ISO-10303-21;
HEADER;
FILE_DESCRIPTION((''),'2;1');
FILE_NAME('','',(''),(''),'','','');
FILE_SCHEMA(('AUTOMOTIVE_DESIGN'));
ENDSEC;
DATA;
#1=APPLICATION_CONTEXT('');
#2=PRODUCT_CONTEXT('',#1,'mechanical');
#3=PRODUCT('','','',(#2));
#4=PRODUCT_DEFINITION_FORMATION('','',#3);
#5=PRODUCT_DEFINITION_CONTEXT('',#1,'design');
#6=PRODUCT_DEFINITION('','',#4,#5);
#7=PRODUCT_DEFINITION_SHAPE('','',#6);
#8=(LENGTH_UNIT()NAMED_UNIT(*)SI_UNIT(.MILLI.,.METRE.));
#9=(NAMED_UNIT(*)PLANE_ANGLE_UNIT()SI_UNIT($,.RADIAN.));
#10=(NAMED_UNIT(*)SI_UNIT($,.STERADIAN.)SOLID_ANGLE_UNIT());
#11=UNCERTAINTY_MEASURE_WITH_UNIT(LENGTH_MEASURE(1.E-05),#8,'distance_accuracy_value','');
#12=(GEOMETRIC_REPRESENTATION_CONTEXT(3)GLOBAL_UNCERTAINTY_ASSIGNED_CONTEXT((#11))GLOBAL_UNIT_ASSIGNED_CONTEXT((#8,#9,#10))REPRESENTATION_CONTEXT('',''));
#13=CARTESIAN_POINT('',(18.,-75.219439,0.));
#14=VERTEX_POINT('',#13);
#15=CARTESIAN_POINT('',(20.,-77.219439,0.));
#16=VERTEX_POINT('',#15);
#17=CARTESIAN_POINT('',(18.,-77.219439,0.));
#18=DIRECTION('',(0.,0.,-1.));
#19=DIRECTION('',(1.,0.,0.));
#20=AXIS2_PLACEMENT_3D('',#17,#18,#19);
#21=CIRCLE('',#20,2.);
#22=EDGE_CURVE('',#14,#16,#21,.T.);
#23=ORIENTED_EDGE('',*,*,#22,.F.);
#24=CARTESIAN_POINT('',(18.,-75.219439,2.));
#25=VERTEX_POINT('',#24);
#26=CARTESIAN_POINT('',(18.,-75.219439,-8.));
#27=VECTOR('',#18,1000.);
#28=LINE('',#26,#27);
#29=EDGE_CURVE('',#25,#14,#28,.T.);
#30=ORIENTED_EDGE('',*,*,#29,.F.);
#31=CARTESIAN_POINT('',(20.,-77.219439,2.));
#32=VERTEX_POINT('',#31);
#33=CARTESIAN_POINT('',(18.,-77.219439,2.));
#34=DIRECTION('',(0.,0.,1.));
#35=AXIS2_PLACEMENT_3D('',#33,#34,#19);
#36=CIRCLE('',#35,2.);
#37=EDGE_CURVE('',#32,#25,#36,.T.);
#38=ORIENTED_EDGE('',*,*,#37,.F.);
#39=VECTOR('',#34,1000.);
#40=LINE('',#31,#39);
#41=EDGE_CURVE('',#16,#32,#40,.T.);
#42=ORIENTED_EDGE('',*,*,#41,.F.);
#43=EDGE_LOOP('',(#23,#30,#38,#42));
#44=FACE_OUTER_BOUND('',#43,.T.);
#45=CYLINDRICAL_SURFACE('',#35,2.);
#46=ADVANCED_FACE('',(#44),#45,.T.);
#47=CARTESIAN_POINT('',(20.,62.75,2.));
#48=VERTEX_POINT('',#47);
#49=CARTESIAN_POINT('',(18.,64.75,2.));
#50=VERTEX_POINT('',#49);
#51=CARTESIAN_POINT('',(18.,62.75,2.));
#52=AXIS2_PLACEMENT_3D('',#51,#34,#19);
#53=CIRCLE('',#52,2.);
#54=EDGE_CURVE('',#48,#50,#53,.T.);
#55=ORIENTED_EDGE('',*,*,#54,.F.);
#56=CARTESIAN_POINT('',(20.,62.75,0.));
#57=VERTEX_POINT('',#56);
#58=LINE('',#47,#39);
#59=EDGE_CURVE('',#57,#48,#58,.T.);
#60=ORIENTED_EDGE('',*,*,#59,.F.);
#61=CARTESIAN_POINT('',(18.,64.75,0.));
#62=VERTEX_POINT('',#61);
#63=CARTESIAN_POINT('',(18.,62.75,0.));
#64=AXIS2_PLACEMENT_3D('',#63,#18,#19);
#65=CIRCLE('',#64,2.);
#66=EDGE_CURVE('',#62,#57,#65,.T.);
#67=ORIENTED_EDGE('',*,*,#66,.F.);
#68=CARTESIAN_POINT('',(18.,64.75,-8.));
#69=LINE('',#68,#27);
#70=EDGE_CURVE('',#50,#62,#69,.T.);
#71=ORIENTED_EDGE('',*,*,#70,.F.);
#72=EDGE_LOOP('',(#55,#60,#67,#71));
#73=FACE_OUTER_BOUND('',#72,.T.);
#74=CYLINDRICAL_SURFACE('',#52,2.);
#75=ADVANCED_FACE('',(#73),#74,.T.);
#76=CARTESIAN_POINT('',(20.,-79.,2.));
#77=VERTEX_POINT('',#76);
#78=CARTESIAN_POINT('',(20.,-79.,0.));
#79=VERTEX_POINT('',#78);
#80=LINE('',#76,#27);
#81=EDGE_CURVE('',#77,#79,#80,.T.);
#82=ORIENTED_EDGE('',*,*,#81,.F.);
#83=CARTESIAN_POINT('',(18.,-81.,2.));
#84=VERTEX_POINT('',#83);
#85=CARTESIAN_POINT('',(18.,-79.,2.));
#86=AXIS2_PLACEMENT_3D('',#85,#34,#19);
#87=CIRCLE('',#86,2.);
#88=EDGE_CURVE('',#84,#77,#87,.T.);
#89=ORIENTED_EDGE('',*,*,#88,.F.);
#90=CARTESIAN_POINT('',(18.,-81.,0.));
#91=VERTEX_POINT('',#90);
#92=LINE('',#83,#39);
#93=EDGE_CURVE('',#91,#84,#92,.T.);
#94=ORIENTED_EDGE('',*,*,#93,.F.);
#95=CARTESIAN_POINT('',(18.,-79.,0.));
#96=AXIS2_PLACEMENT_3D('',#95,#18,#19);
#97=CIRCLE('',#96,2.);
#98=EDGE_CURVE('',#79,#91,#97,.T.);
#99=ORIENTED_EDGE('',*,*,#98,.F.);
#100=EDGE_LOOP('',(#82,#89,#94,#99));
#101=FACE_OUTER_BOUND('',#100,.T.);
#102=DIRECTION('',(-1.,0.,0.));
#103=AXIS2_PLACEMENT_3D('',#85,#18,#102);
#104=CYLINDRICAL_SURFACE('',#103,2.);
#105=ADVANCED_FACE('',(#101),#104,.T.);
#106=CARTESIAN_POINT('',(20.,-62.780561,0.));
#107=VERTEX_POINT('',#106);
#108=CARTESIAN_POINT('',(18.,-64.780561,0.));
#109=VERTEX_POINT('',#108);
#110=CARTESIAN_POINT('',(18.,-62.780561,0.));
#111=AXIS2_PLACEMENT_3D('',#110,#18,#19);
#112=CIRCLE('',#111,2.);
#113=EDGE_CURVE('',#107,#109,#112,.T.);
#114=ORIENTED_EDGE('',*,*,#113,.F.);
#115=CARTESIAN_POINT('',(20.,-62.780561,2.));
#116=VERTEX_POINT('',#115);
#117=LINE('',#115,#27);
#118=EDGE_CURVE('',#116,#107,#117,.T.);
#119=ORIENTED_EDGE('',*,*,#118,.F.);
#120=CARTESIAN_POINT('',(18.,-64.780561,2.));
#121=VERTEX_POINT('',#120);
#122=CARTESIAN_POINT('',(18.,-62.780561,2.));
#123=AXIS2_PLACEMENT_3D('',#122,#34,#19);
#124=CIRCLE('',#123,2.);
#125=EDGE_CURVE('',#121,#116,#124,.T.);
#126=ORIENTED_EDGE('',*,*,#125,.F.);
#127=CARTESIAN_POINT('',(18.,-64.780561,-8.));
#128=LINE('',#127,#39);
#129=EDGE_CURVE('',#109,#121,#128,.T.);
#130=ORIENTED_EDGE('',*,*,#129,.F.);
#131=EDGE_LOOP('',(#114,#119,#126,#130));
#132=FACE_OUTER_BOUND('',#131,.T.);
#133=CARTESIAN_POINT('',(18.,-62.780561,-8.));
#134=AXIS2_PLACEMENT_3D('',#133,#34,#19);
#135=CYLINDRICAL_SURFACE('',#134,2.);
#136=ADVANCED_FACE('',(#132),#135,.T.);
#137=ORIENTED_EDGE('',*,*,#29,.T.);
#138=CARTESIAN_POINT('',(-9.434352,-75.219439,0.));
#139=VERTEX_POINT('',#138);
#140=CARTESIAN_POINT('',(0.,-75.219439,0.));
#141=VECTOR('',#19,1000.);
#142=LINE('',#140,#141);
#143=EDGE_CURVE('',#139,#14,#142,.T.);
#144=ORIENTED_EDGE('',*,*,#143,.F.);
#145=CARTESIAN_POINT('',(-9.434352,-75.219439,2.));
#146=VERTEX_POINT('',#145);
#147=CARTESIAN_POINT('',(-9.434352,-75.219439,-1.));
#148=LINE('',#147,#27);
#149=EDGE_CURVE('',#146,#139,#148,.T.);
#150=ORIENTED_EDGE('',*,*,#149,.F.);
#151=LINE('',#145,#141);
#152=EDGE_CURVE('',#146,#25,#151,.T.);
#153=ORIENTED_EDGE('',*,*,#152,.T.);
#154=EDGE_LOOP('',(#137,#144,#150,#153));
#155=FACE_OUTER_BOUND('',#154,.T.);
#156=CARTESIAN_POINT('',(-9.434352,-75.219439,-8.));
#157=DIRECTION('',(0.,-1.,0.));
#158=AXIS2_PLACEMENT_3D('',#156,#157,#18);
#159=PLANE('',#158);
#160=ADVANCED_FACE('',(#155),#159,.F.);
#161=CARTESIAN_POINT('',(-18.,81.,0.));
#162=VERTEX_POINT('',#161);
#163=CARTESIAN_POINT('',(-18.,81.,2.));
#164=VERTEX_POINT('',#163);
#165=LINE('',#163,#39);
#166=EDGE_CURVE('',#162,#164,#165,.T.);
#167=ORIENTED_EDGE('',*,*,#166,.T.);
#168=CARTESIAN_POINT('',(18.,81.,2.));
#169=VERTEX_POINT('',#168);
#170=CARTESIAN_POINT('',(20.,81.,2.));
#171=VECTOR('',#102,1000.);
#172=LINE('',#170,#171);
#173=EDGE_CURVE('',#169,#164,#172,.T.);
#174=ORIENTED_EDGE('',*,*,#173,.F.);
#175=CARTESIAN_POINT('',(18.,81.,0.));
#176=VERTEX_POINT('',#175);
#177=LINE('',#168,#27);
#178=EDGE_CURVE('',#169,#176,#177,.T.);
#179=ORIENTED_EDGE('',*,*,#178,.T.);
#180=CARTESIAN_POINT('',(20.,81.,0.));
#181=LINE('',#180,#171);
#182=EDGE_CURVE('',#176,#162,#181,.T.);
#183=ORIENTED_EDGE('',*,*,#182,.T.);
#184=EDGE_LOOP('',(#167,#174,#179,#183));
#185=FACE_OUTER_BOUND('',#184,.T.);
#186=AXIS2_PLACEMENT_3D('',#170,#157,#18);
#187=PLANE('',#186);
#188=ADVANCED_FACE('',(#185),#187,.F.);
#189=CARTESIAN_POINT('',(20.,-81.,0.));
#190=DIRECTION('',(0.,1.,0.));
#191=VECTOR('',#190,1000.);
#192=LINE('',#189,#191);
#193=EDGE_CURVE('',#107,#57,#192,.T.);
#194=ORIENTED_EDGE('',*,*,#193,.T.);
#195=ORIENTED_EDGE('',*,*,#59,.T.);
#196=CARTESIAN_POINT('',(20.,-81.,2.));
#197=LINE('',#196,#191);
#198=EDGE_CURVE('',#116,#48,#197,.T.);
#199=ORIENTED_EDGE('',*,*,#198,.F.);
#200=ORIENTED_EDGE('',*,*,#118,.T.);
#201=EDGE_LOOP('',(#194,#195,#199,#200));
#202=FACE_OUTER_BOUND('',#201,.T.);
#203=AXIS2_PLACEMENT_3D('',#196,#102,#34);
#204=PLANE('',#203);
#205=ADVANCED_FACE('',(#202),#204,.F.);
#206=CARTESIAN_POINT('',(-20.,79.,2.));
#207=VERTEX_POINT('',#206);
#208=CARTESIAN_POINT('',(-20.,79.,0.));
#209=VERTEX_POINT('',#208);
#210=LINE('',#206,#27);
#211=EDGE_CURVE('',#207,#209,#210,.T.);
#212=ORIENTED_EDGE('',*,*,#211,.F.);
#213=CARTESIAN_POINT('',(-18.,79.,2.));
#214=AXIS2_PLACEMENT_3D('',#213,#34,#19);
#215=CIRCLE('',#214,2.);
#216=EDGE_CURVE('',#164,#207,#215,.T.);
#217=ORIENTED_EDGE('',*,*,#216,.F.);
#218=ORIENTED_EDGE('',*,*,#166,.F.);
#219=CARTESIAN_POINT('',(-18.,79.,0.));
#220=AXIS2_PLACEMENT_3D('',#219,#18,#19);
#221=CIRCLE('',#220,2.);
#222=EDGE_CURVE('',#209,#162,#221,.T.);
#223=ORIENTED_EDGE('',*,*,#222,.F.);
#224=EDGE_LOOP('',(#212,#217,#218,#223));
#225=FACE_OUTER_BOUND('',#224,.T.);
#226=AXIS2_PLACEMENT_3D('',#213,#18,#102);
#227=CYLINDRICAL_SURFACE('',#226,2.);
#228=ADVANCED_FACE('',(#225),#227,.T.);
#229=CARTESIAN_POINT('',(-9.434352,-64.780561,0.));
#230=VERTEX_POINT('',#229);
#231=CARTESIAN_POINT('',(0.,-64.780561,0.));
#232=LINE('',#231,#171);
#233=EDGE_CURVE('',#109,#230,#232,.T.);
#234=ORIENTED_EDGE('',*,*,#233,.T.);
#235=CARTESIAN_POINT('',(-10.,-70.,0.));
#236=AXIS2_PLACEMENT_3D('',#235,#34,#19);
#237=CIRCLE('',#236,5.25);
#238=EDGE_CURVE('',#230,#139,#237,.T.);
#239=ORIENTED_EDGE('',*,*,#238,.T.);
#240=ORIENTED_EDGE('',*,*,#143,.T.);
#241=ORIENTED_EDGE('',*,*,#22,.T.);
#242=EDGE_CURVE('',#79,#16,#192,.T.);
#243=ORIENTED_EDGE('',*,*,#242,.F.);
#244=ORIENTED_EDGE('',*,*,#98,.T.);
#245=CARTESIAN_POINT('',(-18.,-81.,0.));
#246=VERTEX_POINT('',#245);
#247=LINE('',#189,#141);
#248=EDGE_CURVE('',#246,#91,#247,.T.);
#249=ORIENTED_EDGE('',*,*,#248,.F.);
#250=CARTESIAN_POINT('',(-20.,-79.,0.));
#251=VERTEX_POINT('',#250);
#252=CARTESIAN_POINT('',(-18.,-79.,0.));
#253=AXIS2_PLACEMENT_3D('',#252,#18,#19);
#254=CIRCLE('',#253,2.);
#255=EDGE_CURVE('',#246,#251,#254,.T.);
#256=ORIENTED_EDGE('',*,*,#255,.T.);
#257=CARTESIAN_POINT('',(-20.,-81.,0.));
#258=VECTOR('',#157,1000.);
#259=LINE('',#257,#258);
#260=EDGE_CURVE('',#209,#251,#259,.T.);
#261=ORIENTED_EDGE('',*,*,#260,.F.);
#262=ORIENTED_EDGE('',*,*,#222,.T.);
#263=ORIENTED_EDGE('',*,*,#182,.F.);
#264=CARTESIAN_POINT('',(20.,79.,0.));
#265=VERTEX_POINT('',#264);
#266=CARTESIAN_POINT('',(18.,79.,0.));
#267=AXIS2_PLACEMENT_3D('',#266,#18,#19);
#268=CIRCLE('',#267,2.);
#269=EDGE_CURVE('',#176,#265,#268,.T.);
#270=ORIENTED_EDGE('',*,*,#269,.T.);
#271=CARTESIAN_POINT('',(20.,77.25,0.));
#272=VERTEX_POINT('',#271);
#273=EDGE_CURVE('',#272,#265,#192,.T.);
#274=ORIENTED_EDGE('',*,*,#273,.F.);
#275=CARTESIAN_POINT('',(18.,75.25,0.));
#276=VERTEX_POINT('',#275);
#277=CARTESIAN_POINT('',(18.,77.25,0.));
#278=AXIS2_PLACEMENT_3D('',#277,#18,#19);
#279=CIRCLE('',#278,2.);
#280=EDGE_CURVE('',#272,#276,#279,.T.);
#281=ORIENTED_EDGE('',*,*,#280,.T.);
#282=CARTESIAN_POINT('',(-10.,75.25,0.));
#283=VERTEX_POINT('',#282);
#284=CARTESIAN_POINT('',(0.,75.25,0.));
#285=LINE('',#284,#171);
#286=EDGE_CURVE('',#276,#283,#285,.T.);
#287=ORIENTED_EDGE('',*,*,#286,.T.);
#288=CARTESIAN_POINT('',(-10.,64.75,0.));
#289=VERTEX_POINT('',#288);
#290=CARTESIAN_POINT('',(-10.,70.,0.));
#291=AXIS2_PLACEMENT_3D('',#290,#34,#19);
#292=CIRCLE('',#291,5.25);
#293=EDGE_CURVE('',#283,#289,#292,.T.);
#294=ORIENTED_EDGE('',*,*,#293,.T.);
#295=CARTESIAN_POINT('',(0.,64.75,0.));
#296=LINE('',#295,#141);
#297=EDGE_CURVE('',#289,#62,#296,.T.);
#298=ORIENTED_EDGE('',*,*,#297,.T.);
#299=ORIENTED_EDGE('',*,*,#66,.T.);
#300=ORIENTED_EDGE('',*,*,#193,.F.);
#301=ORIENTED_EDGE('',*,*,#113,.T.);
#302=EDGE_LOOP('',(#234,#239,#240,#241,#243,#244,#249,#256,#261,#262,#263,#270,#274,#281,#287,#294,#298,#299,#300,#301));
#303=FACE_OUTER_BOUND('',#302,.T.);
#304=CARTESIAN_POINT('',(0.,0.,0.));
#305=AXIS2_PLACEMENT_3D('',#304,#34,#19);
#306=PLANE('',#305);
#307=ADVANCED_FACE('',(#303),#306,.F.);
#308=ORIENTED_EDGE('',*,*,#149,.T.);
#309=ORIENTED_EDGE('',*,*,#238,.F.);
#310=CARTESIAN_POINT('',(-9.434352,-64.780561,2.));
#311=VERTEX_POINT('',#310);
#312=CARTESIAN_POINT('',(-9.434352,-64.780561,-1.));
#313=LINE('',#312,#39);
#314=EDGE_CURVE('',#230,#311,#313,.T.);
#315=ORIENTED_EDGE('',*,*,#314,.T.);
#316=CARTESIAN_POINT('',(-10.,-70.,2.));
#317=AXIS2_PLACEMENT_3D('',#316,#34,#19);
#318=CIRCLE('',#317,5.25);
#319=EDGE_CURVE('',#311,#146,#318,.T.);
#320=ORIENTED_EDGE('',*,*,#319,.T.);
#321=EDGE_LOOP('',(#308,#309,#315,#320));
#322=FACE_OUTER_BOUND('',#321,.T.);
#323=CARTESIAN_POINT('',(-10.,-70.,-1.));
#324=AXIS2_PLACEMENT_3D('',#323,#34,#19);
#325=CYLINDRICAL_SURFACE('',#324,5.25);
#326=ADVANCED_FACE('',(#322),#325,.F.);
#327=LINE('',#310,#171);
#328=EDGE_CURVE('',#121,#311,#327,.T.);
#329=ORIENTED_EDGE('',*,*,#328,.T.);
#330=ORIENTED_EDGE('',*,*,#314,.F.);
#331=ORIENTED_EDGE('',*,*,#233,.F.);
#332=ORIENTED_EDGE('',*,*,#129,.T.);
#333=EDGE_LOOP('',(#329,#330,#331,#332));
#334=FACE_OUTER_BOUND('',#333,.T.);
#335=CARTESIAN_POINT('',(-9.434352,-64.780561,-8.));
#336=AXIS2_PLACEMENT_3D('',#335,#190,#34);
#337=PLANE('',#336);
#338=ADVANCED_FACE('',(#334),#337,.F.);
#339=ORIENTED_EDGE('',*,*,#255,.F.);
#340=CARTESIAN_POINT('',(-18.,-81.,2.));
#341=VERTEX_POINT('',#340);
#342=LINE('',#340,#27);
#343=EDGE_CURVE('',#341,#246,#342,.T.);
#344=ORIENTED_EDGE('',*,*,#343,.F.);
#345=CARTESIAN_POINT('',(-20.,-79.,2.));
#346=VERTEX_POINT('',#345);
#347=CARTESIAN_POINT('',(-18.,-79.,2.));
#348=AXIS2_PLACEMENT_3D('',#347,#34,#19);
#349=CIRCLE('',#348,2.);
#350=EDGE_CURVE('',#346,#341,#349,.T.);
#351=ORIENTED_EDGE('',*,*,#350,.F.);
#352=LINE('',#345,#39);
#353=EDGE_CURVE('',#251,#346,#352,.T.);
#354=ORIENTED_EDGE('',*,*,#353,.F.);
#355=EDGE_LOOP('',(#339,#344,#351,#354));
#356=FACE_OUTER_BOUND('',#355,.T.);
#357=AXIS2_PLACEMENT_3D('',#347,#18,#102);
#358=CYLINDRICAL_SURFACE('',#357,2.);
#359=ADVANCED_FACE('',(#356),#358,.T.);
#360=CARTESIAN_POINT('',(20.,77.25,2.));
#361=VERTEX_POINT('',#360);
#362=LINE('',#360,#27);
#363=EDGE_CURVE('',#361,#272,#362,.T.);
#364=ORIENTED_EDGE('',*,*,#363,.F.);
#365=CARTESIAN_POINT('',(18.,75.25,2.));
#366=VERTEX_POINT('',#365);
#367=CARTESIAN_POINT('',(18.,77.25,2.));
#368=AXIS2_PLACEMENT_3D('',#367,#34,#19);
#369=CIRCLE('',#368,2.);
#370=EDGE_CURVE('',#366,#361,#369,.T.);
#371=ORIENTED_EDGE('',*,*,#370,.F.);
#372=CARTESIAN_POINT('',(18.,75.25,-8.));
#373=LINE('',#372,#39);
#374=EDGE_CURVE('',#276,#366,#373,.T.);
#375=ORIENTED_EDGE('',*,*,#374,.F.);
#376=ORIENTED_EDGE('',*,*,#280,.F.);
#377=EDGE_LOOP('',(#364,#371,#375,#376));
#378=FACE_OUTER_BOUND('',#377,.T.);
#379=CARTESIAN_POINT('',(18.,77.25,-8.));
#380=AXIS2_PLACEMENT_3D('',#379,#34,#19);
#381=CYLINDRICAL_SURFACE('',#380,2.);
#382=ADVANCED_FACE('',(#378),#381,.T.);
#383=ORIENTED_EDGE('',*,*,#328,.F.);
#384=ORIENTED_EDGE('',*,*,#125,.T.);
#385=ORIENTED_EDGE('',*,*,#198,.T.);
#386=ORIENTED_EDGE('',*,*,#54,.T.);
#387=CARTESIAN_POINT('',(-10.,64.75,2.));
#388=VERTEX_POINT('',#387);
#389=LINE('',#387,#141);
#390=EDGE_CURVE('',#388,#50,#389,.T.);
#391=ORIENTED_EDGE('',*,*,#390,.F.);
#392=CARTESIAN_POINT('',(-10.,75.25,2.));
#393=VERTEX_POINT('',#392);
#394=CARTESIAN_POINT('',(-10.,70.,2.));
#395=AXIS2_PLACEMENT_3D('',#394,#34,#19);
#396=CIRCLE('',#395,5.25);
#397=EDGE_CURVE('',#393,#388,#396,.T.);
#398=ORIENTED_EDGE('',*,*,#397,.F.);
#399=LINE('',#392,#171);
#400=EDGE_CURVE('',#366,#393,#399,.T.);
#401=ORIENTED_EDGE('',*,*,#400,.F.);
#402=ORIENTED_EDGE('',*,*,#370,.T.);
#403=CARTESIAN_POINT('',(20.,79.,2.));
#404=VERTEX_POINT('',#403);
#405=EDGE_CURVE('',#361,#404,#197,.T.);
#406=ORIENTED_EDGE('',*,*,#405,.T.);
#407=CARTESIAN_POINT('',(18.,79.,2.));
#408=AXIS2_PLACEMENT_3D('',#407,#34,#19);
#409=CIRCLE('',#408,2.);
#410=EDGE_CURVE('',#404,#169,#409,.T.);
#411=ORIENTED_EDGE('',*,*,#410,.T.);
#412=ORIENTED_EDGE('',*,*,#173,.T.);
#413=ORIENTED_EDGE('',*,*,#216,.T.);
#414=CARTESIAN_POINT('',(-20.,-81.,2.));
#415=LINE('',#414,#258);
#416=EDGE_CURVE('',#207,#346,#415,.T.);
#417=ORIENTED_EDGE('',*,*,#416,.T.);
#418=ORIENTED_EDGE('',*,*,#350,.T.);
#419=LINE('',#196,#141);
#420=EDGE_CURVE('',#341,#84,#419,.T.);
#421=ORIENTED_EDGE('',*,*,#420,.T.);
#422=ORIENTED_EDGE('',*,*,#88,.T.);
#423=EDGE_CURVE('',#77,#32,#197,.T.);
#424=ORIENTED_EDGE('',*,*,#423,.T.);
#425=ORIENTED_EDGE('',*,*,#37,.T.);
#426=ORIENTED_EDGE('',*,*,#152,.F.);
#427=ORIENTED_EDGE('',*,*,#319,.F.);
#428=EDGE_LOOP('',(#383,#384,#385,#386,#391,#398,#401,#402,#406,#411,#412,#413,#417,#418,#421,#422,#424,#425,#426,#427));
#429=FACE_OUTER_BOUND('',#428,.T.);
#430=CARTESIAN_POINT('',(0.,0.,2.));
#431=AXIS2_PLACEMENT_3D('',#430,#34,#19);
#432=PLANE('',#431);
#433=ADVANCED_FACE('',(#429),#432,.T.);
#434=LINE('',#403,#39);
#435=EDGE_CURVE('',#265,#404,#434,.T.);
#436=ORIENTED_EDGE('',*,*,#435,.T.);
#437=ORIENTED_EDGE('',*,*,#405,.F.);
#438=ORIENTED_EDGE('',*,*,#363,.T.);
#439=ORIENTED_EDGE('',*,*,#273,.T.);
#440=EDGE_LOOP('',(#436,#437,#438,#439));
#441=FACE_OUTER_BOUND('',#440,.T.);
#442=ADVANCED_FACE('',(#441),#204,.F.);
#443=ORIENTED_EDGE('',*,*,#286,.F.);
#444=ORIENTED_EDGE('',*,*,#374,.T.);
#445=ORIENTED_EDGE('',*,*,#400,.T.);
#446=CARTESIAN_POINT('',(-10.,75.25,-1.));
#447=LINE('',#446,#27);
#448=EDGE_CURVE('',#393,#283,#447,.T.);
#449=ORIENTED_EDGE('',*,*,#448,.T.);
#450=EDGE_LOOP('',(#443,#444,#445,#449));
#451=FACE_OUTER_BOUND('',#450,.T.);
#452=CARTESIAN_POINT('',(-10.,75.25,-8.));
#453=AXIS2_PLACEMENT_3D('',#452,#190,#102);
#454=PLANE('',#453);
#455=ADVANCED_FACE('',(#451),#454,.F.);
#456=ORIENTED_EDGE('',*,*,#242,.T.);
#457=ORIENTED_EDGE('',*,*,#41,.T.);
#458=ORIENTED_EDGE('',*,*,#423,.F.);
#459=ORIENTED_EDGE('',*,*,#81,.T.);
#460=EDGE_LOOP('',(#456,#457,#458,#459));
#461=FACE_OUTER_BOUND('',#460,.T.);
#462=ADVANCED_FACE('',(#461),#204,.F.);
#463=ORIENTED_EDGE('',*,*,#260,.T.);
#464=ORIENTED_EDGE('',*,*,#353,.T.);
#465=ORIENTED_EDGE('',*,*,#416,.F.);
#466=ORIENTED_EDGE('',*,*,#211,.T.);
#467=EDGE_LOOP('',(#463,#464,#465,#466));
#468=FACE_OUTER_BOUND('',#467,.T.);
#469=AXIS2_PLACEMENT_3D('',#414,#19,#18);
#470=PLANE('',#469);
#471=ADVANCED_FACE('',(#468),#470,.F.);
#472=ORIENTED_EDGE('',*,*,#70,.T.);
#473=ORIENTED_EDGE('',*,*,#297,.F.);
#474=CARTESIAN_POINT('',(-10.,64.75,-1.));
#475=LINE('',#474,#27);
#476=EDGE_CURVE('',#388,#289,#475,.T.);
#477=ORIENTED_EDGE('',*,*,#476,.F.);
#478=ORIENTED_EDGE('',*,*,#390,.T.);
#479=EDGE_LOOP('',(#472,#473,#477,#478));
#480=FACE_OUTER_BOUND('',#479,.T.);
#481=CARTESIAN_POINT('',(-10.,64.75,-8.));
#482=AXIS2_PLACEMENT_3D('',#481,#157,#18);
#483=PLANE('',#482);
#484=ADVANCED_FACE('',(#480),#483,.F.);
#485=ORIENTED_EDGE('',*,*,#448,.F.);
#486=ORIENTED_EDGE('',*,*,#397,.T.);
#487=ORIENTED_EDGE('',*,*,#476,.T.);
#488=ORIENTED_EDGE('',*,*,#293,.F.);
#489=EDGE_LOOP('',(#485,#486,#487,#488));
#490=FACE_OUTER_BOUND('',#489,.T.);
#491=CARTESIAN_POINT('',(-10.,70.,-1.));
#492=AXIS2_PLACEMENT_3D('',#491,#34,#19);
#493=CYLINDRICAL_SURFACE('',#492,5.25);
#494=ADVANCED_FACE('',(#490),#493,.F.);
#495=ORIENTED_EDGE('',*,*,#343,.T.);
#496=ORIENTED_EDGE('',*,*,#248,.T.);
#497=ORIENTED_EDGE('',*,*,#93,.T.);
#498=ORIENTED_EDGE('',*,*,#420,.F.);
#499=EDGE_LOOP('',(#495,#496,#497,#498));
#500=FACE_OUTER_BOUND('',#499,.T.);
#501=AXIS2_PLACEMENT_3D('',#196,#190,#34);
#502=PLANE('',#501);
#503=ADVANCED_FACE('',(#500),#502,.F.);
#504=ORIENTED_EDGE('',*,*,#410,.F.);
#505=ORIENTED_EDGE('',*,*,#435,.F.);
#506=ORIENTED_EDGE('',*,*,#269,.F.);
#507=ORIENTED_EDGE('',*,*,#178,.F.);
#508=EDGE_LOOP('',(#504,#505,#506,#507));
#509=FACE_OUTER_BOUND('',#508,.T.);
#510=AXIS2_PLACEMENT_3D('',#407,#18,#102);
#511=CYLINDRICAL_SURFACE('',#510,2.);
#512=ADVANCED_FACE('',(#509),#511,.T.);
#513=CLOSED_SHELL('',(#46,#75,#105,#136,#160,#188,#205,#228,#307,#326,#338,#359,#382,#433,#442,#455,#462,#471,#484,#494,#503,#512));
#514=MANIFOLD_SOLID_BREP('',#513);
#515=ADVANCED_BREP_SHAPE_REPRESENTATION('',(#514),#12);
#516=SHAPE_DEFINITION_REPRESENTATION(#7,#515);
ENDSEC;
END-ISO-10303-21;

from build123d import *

# Parameters (mm, degrees)
SKETCH_1_W          = 40
SKETCH_1_H          = 162
EXTRUDE_1_DEPTH     = 2
SKETCH_2_R          = 5.25
CUT_EXTRUDE_1_DEPTH = 3
SKETCH_4_W          = 30
SKETCH_4_H          = 10.5
SKETCH_4_W_2        = 29.434352085
SKETCH_4_H_2        = 10.438877802
CUT_EXTRUDE_4_DEPTH = 10
FILLET_2_R          = 2


with BuildPart() as part:
    # 草图1 → 凸台-拉伸1 (new body)
    with BuildSketch(Plane.XY):
        Rectangle(SKETCH_1_W, SKETCH_1_H)
    extrude(amount=EXTRUDE_1_DEPTH)

    # 草图2 → 切除-拉伸1 (cut)
    with BuildSketch(Plane.XY.offset(2)):
        with Locations((-10, 70)):
            Circle(SKETCH_2_R)
        with Locations((-10, -70)):
            Circle(SKETCH_2_R)
    extrude(amount=-CUT_EXTRUDE_1_DEPTH, mode=Mode.SUBTRACT)

    # 草图4 → 切除-拉伸4 (cut)
    with BuildSketch(Plane.XY.offset(2)):
        with Locations((5, 70)):
            Rectangle(SKETCH_4_W, SKETCH_4_H)
        with Locations((5.282823957, -70)):
            Rectangle(SKETCH_4_W_2, SKETCH_4_H_2)
    extrude(amount=-CUT_EXTRUDE_4_DEPTH, mode=Mode.SUBTRACT)

    # 圆角2
    fillet_2_edges = [part.edges().sort_by_distance(p)[0] for p in [
        (20, 75.25, 1),
        (20, 64.75, 1),
        (20, -64.780561099, 1),
        (20, -75.219438901, 1),
        (-20, 81, 1),
        (20, 81, 1),
        (20, -81, 1),
        (-20, -81, 1),
    ]]
    fillet(fillet_2_edges, radius=FILLET_2_R)


solid = part.part
